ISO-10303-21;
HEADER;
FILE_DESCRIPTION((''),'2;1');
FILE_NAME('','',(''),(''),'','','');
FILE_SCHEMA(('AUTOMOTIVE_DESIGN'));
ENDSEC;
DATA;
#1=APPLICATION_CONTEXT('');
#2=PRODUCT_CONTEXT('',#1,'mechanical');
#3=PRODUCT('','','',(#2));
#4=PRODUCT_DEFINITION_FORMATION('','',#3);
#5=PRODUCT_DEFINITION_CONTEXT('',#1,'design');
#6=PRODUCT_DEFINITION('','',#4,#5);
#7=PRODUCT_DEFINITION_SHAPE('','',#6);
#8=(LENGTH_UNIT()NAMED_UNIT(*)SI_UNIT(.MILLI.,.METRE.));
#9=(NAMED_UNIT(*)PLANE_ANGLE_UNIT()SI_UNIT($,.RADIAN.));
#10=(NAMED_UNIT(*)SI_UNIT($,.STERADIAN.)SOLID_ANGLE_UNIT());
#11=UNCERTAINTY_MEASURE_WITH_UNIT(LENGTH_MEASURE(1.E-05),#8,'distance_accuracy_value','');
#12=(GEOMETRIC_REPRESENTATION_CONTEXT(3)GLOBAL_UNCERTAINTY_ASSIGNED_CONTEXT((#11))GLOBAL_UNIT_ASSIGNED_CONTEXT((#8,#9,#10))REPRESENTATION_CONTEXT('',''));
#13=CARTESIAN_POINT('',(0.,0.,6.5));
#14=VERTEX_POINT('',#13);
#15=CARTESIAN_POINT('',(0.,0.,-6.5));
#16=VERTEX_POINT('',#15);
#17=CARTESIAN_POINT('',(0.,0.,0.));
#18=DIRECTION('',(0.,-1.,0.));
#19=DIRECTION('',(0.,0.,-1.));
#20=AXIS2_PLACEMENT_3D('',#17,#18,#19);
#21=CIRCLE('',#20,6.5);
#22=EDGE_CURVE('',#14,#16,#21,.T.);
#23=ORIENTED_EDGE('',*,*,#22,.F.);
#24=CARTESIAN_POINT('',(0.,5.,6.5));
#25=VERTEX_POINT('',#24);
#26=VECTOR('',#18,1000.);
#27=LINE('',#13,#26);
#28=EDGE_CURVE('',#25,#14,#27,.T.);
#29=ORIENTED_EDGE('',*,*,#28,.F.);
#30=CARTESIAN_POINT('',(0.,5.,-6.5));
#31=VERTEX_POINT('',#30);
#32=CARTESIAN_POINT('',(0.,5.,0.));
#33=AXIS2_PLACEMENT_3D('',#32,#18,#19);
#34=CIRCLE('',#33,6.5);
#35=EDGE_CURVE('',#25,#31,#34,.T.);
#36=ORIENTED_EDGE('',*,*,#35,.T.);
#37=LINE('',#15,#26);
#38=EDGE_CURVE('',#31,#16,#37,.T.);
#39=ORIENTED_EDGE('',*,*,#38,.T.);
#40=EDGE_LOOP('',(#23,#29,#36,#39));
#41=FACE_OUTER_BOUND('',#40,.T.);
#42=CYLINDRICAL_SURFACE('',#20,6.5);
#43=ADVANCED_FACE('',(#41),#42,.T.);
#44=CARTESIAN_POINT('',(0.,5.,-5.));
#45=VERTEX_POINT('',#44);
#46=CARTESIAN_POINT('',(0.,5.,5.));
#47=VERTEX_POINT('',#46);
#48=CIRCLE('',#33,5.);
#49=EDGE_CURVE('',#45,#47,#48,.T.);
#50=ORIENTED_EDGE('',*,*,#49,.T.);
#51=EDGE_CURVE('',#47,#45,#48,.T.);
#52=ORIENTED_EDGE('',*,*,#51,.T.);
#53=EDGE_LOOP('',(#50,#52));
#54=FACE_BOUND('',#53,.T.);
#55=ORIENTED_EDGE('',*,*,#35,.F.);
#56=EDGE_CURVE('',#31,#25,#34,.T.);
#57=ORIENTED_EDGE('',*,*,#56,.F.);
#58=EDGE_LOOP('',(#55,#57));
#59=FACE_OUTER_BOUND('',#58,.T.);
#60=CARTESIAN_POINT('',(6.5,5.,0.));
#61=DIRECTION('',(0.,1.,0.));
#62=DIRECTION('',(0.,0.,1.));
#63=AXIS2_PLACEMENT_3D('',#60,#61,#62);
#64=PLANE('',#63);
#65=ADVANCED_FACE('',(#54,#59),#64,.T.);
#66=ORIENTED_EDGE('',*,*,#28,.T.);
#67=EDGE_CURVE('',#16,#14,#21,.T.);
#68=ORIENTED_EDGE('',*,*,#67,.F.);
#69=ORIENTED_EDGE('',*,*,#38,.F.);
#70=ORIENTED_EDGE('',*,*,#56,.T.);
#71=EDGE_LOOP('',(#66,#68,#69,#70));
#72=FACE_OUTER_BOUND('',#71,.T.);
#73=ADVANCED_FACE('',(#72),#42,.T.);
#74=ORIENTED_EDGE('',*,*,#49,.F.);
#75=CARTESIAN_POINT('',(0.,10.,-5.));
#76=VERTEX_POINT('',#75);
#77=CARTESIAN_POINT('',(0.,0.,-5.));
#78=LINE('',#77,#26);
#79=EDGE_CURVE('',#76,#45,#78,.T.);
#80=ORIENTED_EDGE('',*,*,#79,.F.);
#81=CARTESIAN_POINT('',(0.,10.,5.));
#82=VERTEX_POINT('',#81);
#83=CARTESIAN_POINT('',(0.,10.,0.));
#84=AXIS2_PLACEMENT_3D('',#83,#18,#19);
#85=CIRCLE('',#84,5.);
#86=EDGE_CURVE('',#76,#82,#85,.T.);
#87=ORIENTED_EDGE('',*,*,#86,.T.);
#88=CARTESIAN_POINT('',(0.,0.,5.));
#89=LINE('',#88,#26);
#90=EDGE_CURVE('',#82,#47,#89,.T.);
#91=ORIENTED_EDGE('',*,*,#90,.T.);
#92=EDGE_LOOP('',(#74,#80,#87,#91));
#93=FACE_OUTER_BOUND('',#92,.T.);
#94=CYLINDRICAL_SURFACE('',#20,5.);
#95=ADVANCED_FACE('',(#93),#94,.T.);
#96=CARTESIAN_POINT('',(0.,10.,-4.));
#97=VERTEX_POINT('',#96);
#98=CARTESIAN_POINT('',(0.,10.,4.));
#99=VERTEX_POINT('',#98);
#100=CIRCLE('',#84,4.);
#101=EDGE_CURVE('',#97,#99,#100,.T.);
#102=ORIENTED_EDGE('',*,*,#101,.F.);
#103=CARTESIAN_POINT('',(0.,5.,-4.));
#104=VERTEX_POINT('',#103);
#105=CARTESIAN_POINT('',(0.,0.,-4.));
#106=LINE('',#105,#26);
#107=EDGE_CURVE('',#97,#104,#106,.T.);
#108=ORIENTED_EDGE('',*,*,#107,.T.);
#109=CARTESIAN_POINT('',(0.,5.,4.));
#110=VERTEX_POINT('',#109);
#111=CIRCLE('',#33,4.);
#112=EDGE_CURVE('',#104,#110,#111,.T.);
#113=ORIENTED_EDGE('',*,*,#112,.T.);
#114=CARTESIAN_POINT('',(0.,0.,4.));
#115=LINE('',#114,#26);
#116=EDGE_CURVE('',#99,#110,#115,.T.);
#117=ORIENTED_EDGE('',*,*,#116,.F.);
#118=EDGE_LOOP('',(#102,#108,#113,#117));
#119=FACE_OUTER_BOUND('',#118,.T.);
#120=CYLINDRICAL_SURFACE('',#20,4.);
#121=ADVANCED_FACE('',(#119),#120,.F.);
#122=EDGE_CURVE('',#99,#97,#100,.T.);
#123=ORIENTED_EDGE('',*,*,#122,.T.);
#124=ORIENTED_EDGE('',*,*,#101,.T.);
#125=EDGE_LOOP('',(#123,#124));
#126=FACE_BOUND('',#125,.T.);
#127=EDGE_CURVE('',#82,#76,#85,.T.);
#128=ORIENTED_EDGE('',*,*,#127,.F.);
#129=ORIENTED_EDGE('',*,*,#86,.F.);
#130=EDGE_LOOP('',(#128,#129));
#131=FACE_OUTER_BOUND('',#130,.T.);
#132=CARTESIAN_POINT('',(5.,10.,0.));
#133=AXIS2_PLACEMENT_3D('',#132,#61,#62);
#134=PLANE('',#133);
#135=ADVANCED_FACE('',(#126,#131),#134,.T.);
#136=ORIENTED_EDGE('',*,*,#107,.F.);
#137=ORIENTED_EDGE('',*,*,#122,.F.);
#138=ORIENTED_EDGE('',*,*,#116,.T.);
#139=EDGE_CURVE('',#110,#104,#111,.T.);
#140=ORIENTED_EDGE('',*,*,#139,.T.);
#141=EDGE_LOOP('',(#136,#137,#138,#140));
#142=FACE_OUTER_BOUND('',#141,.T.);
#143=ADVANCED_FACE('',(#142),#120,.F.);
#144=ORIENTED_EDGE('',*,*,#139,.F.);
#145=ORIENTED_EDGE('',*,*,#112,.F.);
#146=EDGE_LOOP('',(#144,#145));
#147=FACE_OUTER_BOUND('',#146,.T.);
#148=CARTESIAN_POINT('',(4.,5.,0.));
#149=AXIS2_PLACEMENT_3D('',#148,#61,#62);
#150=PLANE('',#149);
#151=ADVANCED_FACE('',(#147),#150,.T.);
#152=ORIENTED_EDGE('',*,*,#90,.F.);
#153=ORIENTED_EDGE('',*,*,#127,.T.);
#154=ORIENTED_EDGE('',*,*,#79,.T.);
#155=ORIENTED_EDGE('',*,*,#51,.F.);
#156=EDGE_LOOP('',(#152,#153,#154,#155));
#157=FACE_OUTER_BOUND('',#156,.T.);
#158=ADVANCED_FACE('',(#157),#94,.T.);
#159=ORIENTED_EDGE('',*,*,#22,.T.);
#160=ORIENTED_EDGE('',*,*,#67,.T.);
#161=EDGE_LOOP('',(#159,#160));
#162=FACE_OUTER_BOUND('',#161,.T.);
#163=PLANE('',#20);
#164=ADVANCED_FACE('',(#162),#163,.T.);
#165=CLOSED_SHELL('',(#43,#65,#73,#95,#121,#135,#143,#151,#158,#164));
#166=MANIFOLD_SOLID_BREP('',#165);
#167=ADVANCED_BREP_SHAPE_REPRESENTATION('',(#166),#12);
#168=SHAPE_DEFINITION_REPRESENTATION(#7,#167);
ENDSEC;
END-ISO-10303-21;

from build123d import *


with BuildPart() as part:
    # Sketch1 → Revolve1 (revolve)
    with BuildSketch(Plane.XY, mode=Mode.PRIVATE) as revolve1_sk:
        Polygon((0, 0), (6.5, 0), (6.5, 5), (5, 5), (5, 10), (4, 10), (4, 5), (0, 5), align=None)
    revolve(revolve1_sk.sketch.rotate(Axis((0, 0, 0), (0, 1, 0)), 90), axis=Axis((0, 0, 0), (0, 1, 0)))


solid = part.part
